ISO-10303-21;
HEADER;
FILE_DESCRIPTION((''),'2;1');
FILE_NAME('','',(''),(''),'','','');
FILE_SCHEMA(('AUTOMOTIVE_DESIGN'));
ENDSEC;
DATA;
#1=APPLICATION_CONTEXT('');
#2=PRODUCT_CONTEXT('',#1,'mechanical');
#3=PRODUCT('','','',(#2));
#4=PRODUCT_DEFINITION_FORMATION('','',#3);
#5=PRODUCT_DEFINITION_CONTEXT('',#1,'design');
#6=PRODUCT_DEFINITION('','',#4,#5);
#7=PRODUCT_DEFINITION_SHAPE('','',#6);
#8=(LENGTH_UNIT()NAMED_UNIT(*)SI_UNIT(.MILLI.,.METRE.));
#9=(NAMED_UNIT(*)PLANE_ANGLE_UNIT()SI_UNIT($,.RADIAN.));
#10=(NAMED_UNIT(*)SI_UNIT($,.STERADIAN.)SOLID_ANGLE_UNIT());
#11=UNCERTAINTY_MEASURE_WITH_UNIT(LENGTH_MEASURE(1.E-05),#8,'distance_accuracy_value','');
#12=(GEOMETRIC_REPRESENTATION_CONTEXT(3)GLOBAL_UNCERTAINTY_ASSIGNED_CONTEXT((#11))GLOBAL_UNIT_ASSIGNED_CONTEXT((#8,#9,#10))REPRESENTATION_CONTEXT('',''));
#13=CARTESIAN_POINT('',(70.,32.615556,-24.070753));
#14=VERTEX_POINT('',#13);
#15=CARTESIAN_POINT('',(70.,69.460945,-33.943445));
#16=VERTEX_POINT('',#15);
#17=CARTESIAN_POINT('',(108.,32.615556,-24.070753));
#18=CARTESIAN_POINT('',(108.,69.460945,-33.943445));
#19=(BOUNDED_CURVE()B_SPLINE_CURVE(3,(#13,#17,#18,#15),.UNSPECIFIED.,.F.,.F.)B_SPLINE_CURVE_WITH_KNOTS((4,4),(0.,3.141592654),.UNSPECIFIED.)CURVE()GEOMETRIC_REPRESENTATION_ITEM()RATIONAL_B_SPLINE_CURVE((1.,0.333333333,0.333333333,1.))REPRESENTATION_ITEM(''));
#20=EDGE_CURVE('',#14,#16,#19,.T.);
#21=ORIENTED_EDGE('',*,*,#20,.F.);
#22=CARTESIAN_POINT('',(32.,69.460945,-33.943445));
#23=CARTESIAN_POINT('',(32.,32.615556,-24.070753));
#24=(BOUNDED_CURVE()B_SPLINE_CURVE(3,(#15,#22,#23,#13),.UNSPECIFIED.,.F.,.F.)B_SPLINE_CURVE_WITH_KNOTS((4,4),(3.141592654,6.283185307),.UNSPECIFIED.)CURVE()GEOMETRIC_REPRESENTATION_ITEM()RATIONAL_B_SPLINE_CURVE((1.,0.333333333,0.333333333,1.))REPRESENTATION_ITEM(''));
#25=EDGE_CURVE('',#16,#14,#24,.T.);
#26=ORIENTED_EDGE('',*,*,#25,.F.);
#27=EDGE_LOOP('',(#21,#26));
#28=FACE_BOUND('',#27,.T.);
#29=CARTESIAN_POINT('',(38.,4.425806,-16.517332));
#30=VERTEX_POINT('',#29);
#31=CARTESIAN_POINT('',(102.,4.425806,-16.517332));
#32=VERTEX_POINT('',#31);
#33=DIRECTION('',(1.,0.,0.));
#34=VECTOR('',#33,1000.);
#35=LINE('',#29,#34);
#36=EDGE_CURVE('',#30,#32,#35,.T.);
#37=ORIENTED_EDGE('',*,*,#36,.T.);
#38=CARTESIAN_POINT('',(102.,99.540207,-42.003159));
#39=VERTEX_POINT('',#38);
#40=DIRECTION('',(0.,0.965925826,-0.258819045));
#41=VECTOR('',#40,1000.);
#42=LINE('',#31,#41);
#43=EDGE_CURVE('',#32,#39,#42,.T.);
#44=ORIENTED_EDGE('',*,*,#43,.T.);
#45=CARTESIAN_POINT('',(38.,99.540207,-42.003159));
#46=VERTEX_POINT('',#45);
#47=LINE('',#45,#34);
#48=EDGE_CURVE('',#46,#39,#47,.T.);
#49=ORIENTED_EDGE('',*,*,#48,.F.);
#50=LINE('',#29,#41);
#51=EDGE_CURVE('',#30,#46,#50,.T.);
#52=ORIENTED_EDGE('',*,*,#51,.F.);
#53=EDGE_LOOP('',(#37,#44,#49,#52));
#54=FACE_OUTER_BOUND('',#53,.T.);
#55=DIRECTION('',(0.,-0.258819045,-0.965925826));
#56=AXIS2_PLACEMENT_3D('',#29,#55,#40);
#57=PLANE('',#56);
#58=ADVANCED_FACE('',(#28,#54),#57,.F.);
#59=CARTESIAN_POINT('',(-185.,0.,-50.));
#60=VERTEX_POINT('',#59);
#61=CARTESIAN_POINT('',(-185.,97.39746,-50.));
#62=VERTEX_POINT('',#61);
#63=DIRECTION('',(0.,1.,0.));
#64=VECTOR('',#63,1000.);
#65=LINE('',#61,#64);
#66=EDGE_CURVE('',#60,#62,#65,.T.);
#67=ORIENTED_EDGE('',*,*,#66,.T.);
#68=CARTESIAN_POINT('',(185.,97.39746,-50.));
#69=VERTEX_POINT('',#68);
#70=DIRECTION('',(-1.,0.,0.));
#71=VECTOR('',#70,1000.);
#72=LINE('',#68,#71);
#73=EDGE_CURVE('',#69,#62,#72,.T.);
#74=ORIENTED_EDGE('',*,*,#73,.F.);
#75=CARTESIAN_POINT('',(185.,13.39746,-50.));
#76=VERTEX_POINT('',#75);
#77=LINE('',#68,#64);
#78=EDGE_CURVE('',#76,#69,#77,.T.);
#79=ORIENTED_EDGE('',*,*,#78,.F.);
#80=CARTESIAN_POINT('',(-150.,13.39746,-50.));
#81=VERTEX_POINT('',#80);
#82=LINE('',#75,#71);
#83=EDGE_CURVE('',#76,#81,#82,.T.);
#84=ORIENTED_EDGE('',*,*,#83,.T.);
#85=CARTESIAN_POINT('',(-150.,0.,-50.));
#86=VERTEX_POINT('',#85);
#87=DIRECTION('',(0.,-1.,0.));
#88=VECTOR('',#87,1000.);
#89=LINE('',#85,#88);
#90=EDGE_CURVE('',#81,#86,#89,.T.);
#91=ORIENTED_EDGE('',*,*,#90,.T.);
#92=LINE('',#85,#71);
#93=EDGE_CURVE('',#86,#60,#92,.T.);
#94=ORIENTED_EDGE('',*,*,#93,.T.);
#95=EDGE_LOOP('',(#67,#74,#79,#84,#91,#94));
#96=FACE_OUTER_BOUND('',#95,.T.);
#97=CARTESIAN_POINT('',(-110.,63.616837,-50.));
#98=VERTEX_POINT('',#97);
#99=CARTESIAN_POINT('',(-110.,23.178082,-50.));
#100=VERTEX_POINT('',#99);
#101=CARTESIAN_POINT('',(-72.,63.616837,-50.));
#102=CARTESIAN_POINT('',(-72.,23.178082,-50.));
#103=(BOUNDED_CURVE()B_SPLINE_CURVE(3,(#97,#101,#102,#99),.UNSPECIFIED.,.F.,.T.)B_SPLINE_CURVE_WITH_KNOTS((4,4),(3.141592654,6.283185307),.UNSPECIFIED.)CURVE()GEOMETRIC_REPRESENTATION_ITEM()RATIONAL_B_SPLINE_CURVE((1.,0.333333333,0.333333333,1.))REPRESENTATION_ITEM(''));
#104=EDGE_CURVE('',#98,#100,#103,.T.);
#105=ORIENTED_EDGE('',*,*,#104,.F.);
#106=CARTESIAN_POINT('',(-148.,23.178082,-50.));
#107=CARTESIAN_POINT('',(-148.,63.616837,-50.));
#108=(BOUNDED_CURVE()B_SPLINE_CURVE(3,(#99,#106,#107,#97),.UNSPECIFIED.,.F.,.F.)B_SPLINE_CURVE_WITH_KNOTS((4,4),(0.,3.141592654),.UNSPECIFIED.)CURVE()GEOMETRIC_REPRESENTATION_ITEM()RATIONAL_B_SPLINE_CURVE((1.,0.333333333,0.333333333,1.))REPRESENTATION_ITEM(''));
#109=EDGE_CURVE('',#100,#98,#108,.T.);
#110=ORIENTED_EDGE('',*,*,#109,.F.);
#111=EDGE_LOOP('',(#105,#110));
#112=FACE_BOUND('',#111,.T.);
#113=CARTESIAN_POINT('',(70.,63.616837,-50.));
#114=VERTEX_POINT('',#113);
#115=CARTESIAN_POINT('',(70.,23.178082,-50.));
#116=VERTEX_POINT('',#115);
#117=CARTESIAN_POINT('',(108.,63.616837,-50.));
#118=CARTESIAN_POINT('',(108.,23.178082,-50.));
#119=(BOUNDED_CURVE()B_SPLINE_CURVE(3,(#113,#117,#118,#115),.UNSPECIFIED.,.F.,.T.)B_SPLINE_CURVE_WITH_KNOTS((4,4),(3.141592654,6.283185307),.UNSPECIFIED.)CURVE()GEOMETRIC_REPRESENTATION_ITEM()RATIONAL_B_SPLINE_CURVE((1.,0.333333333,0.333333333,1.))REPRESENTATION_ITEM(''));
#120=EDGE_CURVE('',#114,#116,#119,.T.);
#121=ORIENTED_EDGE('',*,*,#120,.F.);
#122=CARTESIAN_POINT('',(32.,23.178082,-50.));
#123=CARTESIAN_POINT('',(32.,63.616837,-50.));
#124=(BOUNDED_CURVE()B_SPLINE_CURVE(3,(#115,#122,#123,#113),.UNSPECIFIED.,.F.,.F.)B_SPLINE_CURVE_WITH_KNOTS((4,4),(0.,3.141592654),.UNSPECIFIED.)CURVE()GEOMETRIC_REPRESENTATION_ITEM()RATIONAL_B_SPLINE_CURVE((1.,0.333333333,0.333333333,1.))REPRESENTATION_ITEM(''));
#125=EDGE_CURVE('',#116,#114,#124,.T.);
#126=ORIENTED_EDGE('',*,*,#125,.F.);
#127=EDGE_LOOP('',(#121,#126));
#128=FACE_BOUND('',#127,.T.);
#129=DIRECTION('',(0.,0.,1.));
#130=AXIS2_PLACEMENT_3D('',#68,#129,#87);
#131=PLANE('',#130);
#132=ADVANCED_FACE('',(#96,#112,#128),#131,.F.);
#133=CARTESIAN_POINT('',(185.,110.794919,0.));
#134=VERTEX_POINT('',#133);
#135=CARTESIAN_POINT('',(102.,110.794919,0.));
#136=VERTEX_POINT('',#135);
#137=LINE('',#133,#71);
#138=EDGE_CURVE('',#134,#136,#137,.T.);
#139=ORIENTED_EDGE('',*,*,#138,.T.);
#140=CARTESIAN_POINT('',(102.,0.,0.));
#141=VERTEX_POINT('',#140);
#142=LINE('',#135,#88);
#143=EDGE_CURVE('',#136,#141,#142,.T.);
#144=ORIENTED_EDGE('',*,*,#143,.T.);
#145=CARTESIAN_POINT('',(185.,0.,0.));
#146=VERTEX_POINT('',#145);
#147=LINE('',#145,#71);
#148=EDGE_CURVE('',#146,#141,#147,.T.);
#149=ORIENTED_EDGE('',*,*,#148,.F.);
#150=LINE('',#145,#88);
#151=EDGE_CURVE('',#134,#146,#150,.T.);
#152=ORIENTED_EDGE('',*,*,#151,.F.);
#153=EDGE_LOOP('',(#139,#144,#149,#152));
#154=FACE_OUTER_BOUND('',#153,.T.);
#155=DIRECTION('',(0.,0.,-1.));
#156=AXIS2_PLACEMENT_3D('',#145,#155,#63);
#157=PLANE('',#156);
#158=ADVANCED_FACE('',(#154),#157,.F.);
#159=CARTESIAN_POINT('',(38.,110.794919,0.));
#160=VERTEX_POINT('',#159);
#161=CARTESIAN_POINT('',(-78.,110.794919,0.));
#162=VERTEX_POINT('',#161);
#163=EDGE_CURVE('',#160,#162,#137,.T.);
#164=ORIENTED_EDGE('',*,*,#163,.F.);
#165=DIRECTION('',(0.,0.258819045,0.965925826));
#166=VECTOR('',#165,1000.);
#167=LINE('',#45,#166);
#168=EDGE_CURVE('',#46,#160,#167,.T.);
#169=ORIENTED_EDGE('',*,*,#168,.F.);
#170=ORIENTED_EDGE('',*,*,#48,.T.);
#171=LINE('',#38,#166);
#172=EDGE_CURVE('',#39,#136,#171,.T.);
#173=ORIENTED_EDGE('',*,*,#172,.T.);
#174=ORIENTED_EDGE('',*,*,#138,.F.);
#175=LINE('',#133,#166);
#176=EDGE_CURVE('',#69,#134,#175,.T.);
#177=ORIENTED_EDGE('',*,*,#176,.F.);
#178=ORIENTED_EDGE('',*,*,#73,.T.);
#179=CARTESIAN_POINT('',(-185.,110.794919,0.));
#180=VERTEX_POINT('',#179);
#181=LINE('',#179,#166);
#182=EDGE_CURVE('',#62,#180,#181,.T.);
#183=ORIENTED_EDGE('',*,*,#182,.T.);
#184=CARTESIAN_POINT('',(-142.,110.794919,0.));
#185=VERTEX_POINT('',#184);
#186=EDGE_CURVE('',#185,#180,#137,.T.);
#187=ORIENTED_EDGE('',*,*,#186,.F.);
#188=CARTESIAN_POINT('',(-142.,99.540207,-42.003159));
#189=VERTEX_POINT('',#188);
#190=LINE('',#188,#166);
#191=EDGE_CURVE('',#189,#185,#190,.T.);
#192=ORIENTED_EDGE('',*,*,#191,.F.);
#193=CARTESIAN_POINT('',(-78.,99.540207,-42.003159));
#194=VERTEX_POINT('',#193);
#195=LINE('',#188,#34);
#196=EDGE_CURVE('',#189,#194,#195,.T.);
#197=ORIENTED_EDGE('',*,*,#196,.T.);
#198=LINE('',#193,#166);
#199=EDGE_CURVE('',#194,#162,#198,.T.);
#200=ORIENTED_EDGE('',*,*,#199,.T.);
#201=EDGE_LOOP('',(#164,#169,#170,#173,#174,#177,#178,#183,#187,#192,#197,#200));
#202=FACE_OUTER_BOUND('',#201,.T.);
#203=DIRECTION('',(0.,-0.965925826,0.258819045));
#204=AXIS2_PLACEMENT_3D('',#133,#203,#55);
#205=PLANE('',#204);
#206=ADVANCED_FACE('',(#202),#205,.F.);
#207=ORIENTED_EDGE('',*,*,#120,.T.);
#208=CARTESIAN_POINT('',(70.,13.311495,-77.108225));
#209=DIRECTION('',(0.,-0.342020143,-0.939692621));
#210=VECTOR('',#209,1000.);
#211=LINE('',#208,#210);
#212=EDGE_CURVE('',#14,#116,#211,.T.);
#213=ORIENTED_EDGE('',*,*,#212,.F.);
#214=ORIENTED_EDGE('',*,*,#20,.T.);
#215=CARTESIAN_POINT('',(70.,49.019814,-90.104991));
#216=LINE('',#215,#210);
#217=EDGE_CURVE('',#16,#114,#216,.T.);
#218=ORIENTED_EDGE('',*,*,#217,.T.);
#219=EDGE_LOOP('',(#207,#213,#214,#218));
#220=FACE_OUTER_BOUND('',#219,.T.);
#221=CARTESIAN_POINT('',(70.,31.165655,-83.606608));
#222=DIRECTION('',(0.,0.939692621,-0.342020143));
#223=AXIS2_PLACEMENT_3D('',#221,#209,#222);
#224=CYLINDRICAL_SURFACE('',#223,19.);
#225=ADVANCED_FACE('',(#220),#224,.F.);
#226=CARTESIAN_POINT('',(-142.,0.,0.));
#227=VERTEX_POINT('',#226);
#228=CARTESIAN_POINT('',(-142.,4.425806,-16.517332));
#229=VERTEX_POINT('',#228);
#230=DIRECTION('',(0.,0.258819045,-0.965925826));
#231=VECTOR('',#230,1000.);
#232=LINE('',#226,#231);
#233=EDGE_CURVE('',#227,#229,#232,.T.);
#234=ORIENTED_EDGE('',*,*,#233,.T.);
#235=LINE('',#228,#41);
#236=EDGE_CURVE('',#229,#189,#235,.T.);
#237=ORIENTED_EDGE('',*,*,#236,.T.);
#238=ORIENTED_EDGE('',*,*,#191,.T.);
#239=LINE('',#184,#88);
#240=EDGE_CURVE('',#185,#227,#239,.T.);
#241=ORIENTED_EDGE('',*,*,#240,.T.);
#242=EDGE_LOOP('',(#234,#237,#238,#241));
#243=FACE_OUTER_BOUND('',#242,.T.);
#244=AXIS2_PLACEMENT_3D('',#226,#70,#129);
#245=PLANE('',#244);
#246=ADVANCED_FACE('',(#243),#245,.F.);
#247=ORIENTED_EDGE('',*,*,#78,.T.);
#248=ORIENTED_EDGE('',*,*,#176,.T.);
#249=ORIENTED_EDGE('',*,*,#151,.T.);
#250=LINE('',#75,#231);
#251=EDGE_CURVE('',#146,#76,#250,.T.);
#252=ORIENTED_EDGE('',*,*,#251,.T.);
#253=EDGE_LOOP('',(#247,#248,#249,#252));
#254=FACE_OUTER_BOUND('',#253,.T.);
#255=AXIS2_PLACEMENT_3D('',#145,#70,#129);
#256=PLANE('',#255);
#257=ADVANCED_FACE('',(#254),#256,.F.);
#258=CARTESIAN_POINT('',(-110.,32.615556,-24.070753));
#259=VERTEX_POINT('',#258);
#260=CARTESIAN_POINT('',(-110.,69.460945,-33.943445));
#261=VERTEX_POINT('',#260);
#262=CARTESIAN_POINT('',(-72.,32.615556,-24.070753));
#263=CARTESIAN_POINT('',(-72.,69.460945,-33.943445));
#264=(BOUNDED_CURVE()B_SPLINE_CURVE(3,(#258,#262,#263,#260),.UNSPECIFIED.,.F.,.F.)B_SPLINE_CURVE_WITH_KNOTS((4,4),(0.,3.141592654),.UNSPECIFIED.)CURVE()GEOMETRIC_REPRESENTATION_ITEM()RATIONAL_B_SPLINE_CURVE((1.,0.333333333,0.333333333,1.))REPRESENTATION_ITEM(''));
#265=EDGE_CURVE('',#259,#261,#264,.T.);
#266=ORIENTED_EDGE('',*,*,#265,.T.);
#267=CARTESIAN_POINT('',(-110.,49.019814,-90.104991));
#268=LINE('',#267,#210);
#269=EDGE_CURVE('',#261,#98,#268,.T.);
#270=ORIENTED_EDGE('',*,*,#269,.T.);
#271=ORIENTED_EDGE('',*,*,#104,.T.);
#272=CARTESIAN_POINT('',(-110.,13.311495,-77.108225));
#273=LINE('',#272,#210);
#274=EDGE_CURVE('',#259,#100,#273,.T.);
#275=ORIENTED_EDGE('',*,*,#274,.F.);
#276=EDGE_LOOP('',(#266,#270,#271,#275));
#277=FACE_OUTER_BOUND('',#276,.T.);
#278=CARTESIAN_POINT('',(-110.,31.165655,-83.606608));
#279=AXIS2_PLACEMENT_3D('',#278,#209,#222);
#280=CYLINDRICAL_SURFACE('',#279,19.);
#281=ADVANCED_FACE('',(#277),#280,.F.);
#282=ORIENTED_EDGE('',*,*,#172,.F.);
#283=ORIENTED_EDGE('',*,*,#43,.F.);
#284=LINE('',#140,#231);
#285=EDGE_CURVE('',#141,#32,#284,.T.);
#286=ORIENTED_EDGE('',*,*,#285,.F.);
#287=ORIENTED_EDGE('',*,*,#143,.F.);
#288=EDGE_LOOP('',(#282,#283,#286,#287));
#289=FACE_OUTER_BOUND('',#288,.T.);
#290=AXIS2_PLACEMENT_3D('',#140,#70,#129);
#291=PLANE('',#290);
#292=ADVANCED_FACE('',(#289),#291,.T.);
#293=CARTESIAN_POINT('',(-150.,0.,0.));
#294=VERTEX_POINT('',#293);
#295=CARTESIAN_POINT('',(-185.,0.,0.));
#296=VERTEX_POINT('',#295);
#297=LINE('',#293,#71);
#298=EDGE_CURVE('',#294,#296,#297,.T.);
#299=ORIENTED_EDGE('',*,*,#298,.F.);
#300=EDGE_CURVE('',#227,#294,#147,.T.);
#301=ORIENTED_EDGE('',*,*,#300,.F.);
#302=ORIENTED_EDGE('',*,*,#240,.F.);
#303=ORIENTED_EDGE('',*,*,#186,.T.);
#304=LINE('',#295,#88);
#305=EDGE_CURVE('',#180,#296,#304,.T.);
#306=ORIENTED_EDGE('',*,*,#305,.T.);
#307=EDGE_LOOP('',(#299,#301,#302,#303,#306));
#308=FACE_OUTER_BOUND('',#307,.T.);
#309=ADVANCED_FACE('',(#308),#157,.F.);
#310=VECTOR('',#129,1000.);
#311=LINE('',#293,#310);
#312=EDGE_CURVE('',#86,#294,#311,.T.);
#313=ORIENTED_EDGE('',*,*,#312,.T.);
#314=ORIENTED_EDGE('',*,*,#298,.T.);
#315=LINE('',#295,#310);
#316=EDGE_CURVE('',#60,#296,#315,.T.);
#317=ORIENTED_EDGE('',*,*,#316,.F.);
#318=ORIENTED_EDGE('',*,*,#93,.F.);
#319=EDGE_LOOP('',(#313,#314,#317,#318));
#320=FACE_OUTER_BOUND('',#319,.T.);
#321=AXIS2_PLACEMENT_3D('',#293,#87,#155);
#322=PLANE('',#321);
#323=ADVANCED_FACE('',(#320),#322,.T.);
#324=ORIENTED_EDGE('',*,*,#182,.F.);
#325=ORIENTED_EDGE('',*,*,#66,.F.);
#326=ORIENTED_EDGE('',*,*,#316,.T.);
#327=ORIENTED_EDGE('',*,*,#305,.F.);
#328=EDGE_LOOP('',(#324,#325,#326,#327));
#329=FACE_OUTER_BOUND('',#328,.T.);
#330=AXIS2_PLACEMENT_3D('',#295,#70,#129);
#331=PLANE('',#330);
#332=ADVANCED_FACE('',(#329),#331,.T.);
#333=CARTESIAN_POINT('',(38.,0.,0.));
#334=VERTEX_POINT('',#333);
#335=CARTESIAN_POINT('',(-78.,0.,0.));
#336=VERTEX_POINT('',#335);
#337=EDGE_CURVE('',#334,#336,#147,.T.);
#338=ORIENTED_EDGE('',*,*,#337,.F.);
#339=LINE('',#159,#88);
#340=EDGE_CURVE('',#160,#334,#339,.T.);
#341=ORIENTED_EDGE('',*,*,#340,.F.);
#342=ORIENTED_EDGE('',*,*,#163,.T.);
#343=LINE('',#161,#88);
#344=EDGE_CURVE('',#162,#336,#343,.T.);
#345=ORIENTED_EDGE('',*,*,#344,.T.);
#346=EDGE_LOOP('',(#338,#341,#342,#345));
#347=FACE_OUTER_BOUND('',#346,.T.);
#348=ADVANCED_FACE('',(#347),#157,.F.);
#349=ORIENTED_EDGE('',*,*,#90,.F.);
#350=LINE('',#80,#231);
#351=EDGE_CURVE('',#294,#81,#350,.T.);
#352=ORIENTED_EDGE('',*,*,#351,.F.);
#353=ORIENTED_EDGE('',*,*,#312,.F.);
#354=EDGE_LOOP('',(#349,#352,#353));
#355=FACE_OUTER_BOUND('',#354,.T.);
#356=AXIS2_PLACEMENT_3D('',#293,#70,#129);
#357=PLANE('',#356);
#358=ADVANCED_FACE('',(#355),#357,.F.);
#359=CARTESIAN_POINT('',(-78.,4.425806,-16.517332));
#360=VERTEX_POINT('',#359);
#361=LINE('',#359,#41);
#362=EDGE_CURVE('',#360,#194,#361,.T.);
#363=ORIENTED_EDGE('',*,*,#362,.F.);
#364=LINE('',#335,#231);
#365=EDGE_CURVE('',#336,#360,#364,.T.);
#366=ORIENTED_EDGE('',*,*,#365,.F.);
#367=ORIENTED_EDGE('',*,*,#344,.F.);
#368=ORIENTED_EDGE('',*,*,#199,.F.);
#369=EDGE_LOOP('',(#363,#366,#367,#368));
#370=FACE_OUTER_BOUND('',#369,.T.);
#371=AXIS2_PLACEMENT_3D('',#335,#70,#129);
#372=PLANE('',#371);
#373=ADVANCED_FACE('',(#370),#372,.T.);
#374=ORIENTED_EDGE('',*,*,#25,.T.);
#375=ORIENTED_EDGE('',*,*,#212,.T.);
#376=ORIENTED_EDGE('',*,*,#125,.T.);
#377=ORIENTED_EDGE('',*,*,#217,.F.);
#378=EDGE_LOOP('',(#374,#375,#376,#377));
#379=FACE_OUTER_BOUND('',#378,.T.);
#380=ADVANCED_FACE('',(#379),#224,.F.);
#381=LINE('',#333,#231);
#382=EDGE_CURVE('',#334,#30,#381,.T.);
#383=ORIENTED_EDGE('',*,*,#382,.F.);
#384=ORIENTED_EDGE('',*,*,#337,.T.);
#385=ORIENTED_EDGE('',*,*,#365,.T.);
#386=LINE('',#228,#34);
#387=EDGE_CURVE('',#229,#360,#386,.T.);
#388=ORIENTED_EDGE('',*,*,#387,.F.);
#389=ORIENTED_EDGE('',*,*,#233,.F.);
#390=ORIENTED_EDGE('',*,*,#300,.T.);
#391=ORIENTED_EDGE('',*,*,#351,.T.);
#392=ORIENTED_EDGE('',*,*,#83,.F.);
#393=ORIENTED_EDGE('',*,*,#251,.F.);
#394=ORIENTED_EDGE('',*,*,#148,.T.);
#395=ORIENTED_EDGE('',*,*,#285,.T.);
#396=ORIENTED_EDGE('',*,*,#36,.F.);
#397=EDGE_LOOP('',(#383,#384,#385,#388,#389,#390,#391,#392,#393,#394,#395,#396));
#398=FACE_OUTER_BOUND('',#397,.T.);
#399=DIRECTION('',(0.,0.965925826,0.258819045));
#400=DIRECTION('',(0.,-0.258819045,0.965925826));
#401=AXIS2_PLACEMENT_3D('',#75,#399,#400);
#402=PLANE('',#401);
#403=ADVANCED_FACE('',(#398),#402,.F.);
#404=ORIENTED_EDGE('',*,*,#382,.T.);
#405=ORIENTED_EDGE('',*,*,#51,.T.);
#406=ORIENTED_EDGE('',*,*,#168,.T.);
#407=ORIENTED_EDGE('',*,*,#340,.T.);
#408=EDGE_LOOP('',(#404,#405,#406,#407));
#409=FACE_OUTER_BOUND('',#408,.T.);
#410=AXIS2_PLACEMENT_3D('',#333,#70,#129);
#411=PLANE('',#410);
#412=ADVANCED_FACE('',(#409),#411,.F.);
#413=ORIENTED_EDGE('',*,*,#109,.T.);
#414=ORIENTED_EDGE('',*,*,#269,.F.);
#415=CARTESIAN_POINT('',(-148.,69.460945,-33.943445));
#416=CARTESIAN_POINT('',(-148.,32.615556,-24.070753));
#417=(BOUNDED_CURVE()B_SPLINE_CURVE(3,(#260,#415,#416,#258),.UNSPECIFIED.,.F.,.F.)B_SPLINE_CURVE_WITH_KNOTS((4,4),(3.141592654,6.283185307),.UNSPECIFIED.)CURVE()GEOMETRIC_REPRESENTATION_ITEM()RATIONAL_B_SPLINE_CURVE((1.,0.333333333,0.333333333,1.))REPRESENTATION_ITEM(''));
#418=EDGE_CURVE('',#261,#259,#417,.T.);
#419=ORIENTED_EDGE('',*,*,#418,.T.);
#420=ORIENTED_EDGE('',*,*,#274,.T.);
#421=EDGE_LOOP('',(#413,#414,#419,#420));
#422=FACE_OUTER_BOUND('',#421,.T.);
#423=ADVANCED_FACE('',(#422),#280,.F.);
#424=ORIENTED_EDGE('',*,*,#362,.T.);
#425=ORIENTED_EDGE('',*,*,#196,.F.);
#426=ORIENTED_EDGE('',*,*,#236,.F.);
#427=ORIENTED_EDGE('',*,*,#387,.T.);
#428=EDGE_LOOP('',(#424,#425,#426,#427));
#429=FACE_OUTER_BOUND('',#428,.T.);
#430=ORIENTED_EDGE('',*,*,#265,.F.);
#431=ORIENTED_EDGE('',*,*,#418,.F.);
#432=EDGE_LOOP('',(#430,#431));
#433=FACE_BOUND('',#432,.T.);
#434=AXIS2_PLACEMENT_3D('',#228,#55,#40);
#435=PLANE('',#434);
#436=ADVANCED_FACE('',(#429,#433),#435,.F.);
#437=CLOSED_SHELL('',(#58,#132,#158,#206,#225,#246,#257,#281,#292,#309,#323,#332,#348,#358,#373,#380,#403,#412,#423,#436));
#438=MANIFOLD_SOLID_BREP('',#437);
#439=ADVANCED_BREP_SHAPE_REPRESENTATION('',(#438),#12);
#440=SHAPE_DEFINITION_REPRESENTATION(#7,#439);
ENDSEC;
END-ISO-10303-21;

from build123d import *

# Parameters (mm, degrees)
BOSS_EXTRUDE1_DEPTH = 185
BOSS_EXTRUDE2_DEPTH = 35
CUT_EXTRUDE1_START  = -110
CUT_EXTRUDE1_DEPTH  = 32
CUT_EXTRUDE2_START  = 70
CUT_EXTRUDE2_DEPTH  = 32
SKETCH6_W           = 76.501144457
SKETCH6_H           = 19
LPATTERN1_COUNT     = 2
LPATTERN1_PITCH     = 180


with BuildPart() as part:
    # Sketch1 → Boss-Extrude1 (new, symmetric)
    with BuildSketch(Plane(origin=(0, 0, 0), x_dir=(0, 0, -1), z_dir=(1, 0, 0))):
        Polygon((0, 0), (0, 110.794919243), (50, 97.397459622), (50, 13.397459622), align=None)
    extrude(amount=BOSS_EXTRUDE1_DEPTH, both=True)

    # Sketch2 → Boss-Extrude2 (add)
    with BuildSketch(Plane.ZY.offset(185)):
        Polygon((0, 0), (-50, 0), (-50, 13.397459622), align=None)
    extrude(amount=-BOSS_EXTRUDE2_DEPTH)

    # Sketch3 → Cut-Extrude1 (cut, symmetric)
    with BuildSketch(Plane(origin=(0, 0, 0), x_dir=(0, 0, -1), z_dir=(1, 0, 0)).offset(CUT_EXTRUDE1_START)):
        Polygon((16.51733163, 4.425805671), (42.003158605, 99.540206815), (0, 110.794919243), (0, 0), align=None)
    extrude(amount=CUT_EXTRUDE1_DEPTH, both=True, mode=Mode.SUBTRACT)

    # Sketch4 → Cut-Extrude2 (cut, symmetric)
    with BuildSketch(Plane(origin=(0, 0, 0), x_dir=(0, 0, -1), z_dir=(1, 0, 0)).offset(CUT_EXTRUDE2_START)):
        Polygon((16.51733163, 4.425805671), (42.003158605, 99.540206815), (0, 110.794919243), (0, 0), align=None)
    extrude(amount=CUT_EXTRUDE2_DEPTH, both=True, mode=Mode.SUBTRACT)

    # Sketch6 → Cut-Revolve1 (revolve, cut)
    with BuildSketch(Plane(origin=(0, 54.390611447, -19.79656359), x_dir=(0, 0.342020143325663, 0.9396926207859105), z_dir=(0, 0.9396926207859105, -0.342020143325663)), mode=Mode.PRIVATE) as cut_revolve1_sk:
        with Locations((-25.35224184, -100.5)):
            Rectangle(SKETCH6_W, SKETCH6_H)
    cut_revolve1 = revolve(cut_revolve1_sk.sketch.rotate(Axis((-110, 31.16565465, -83.606607958), (0, 0.342020143325663, 0.9396926207859105)), 270), axis=Axis((-110, 31.16565465, -83.606607958), (0, 0.342020143325663, 0.9396926207859105)), mode=Mode.SUBTRACT)

    # LPattern1: Cut-Revolve1 ×2
    with Locations(*[(i * LPATTERN1_PITCH, 0, 0) for i in range(1, LPATTERN1_COUNT)]):
        add(cut_revolve1, mode=Mode.SUBTRACT)


solid = part.part
